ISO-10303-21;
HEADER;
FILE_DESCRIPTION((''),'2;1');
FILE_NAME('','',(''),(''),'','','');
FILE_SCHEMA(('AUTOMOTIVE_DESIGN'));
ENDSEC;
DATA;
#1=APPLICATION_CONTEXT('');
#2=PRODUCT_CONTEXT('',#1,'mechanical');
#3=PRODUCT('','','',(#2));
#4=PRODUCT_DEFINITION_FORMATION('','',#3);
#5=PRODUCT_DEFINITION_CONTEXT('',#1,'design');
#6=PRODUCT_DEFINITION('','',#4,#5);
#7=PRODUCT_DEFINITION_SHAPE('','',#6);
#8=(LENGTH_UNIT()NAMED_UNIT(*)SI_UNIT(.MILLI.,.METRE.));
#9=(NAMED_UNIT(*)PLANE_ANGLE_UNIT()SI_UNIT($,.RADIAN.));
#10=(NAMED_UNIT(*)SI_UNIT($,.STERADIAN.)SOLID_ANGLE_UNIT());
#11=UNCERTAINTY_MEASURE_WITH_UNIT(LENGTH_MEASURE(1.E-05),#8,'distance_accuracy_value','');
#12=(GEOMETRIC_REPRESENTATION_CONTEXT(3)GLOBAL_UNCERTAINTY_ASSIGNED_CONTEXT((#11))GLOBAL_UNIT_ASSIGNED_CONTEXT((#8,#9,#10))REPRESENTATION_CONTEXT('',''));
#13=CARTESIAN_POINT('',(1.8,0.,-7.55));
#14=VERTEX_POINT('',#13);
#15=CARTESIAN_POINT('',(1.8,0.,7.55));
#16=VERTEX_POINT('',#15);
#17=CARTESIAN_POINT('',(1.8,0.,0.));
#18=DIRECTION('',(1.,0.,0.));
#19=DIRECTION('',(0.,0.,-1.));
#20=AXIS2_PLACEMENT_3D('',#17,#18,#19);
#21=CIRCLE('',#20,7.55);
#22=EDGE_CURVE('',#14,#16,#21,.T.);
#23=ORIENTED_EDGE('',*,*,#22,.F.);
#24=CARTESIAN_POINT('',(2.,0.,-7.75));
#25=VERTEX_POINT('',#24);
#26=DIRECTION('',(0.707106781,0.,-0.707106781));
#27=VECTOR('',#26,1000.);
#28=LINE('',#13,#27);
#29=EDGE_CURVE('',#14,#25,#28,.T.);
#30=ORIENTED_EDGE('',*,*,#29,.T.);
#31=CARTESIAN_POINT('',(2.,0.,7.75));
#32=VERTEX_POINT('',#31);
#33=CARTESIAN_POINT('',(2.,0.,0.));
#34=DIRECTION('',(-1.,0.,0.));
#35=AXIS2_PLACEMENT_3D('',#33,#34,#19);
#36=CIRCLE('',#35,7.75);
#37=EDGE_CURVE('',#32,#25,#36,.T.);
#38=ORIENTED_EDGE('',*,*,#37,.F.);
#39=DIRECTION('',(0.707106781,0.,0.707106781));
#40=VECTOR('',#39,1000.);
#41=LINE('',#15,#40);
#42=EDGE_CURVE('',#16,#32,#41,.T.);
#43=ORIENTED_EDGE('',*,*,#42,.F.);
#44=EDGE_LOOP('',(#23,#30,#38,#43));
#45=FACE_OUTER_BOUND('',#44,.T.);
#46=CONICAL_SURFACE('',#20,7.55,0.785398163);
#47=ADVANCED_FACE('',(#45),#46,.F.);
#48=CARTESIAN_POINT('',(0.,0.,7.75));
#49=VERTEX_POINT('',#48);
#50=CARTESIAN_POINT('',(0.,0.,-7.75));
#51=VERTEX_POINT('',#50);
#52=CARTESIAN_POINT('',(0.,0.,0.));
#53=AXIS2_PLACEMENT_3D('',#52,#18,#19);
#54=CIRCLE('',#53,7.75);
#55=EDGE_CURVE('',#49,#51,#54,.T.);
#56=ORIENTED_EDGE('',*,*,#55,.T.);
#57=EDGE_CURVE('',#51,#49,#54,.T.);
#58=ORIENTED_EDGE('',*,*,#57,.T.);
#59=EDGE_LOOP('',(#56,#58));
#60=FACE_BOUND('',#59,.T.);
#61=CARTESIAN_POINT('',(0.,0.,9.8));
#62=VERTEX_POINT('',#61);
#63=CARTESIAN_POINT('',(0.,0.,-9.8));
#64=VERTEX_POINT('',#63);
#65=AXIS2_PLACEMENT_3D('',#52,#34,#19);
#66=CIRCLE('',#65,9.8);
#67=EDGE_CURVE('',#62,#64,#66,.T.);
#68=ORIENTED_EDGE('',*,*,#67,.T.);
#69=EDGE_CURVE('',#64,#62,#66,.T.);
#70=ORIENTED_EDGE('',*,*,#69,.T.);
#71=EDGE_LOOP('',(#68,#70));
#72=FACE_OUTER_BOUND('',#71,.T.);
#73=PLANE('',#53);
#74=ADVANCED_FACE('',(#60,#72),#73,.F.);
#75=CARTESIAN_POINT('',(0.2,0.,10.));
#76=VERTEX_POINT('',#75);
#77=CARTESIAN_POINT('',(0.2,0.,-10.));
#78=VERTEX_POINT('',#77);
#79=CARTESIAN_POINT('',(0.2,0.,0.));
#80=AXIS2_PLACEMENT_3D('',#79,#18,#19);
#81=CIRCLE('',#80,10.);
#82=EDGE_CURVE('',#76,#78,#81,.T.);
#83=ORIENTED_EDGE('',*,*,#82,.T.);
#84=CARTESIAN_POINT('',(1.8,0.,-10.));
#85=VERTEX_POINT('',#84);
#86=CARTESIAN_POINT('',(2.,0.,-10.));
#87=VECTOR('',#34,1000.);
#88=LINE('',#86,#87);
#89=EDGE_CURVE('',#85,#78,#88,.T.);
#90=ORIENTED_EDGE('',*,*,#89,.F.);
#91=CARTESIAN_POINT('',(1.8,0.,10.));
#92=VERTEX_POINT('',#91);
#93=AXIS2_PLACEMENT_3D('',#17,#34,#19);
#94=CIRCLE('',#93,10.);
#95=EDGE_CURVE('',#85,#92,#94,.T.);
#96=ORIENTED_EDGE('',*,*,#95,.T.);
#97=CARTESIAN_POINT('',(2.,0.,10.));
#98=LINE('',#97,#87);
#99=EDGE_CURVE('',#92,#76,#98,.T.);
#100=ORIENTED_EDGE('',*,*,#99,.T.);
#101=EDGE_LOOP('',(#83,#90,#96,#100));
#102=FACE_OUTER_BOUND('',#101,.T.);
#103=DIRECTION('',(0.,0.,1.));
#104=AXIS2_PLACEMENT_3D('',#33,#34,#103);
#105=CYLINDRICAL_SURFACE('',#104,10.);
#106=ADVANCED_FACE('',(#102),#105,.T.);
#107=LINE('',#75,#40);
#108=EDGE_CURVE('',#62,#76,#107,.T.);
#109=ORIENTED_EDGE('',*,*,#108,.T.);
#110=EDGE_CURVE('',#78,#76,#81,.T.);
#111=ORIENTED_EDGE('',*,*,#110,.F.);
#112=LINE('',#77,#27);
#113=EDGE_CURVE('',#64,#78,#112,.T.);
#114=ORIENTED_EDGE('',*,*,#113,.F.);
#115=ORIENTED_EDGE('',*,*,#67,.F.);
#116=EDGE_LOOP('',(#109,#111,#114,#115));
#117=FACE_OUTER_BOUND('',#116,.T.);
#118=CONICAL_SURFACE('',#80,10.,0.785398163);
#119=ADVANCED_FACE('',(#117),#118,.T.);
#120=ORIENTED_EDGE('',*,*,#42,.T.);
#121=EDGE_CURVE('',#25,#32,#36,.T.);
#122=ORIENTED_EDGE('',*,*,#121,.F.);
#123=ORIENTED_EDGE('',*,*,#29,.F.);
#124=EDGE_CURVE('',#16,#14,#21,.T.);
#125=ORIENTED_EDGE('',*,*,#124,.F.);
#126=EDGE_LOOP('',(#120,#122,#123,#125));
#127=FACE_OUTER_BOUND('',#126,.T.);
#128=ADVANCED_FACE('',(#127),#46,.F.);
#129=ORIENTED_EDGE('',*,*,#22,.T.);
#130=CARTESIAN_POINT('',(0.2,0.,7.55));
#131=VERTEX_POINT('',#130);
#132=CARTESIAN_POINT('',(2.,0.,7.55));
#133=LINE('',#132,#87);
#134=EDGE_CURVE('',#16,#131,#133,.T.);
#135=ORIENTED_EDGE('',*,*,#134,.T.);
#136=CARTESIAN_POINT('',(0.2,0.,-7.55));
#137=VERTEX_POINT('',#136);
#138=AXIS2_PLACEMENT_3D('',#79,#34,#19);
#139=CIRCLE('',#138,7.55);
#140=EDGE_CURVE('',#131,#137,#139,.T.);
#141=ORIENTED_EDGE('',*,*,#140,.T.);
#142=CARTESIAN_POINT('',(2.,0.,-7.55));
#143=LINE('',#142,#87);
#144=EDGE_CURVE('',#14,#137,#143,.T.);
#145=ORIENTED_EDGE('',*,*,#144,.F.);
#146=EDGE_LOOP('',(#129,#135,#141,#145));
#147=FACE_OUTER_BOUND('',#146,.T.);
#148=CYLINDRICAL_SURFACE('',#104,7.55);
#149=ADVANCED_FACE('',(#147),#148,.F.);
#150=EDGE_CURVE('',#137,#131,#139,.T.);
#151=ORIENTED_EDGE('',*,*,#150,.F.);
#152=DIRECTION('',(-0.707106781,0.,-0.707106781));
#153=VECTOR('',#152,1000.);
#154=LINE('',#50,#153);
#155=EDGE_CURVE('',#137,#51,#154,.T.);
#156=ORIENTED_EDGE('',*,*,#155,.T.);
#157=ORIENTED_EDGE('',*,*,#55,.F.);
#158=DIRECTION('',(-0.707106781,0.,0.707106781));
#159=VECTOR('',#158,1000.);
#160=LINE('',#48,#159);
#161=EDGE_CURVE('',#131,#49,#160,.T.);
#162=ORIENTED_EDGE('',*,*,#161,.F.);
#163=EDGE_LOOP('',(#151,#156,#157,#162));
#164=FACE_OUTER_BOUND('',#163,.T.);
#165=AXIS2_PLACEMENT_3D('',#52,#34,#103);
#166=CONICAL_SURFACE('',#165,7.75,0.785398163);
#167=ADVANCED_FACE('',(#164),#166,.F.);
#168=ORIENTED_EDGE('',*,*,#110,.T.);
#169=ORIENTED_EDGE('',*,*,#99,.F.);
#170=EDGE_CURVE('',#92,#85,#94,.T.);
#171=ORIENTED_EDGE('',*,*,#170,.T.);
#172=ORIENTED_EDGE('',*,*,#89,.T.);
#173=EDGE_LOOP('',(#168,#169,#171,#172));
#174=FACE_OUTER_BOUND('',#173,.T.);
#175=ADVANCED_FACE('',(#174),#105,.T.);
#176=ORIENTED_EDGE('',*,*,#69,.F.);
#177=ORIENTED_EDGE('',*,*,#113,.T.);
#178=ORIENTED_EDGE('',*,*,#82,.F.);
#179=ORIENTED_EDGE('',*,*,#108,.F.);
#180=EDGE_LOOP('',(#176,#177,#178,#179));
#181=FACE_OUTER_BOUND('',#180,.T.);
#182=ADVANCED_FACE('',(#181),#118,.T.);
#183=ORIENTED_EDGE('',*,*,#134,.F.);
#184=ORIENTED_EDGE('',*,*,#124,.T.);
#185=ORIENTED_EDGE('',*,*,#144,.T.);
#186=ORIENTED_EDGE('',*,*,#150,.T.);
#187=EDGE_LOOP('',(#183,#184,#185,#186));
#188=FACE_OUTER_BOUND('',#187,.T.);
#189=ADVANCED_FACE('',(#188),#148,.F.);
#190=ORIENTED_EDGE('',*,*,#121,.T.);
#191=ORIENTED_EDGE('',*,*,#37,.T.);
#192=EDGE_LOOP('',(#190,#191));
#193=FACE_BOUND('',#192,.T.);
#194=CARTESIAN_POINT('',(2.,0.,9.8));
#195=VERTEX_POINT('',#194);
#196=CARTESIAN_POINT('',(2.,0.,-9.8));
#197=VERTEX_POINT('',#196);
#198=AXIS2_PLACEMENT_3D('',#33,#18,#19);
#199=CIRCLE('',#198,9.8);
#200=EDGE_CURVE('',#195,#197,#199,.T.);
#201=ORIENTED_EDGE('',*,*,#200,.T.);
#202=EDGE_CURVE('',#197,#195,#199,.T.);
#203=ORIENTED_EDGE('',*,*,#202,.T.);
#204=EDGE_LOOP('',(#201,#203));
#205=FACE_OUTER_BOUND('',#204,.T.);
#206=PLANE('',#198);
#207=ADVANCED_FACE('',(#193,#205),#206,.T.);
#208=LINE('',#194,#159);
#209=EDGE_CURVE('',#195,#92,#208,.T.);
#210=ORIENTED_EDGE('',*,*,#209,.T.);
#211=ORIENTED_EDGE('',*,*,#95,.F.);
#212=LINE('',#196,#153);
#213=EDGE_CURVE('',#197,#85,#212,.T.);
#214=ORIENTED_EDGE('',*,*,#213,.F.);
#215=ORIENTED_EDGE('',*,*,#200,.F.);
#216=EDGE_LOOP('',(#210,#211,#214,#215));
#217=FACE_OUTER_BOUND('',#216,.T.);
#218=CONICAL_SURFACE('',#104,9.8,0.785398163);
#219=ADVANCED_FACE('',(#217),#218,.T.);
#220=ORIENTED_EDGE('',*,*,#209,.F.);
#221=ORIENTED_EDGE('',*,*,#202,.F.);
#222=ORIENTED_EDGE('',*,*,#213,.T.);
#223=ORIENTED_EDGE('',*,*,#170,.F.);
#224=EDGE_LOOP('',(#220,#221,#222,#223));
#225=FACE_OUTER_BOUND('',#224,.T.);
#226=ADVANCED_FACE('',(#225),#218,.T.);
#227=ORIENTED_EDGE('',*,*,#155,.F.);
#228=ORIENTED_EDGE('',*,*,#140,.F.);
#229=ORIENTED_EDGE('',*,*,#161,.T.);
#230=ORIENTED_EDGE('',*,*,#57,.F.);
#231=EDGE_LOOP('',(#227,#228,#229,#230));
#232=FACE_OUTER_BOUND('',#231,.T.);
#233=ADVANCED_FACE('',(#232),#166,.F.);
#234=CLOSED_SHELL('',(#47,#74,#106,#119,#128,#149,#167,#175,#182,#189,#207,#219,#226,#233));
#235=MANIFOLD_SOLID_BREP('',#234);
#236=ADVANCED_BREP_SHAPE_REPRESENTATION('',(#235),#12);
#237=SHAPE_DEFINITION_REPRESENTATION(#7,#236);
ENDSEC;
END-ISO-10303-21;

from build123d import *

# Parameters (mm, degrees)
SKETCH_1_R      = 10
SKETCH_1_R_2    = 7.55
EXTRUDE_1_DEPTH = 2
CHAMFER_1_SIZE  = 0.2


with BuildPart() as part:
    # 草图1 → 凸台-拉伸1 (new body)
    with BuildSketch(Plane(origin=(0, 0, 0), x_dir=(0, 0, -1), z_dir=(1, 0, 0))):
        Circle(SKETCH_1_R)
        Circle(SKETCH_1_R_2, mode=Mode.SUBTRACT)
    extrude(amount=EXTRUDE_1_DEPTH)

    # 倒角1
    chamfer_1_edges = [part.edges().sort_by_distance(p)[0] for p in [
        (0, 0, 10),
        (2, 0, 10),
        (0, 0, 7.55),
        (2, 0, 7.55),
    ]]
    chamfer(chamfer_1_edges, length=CHAMFER_1_SIZE)


solid = part.part
